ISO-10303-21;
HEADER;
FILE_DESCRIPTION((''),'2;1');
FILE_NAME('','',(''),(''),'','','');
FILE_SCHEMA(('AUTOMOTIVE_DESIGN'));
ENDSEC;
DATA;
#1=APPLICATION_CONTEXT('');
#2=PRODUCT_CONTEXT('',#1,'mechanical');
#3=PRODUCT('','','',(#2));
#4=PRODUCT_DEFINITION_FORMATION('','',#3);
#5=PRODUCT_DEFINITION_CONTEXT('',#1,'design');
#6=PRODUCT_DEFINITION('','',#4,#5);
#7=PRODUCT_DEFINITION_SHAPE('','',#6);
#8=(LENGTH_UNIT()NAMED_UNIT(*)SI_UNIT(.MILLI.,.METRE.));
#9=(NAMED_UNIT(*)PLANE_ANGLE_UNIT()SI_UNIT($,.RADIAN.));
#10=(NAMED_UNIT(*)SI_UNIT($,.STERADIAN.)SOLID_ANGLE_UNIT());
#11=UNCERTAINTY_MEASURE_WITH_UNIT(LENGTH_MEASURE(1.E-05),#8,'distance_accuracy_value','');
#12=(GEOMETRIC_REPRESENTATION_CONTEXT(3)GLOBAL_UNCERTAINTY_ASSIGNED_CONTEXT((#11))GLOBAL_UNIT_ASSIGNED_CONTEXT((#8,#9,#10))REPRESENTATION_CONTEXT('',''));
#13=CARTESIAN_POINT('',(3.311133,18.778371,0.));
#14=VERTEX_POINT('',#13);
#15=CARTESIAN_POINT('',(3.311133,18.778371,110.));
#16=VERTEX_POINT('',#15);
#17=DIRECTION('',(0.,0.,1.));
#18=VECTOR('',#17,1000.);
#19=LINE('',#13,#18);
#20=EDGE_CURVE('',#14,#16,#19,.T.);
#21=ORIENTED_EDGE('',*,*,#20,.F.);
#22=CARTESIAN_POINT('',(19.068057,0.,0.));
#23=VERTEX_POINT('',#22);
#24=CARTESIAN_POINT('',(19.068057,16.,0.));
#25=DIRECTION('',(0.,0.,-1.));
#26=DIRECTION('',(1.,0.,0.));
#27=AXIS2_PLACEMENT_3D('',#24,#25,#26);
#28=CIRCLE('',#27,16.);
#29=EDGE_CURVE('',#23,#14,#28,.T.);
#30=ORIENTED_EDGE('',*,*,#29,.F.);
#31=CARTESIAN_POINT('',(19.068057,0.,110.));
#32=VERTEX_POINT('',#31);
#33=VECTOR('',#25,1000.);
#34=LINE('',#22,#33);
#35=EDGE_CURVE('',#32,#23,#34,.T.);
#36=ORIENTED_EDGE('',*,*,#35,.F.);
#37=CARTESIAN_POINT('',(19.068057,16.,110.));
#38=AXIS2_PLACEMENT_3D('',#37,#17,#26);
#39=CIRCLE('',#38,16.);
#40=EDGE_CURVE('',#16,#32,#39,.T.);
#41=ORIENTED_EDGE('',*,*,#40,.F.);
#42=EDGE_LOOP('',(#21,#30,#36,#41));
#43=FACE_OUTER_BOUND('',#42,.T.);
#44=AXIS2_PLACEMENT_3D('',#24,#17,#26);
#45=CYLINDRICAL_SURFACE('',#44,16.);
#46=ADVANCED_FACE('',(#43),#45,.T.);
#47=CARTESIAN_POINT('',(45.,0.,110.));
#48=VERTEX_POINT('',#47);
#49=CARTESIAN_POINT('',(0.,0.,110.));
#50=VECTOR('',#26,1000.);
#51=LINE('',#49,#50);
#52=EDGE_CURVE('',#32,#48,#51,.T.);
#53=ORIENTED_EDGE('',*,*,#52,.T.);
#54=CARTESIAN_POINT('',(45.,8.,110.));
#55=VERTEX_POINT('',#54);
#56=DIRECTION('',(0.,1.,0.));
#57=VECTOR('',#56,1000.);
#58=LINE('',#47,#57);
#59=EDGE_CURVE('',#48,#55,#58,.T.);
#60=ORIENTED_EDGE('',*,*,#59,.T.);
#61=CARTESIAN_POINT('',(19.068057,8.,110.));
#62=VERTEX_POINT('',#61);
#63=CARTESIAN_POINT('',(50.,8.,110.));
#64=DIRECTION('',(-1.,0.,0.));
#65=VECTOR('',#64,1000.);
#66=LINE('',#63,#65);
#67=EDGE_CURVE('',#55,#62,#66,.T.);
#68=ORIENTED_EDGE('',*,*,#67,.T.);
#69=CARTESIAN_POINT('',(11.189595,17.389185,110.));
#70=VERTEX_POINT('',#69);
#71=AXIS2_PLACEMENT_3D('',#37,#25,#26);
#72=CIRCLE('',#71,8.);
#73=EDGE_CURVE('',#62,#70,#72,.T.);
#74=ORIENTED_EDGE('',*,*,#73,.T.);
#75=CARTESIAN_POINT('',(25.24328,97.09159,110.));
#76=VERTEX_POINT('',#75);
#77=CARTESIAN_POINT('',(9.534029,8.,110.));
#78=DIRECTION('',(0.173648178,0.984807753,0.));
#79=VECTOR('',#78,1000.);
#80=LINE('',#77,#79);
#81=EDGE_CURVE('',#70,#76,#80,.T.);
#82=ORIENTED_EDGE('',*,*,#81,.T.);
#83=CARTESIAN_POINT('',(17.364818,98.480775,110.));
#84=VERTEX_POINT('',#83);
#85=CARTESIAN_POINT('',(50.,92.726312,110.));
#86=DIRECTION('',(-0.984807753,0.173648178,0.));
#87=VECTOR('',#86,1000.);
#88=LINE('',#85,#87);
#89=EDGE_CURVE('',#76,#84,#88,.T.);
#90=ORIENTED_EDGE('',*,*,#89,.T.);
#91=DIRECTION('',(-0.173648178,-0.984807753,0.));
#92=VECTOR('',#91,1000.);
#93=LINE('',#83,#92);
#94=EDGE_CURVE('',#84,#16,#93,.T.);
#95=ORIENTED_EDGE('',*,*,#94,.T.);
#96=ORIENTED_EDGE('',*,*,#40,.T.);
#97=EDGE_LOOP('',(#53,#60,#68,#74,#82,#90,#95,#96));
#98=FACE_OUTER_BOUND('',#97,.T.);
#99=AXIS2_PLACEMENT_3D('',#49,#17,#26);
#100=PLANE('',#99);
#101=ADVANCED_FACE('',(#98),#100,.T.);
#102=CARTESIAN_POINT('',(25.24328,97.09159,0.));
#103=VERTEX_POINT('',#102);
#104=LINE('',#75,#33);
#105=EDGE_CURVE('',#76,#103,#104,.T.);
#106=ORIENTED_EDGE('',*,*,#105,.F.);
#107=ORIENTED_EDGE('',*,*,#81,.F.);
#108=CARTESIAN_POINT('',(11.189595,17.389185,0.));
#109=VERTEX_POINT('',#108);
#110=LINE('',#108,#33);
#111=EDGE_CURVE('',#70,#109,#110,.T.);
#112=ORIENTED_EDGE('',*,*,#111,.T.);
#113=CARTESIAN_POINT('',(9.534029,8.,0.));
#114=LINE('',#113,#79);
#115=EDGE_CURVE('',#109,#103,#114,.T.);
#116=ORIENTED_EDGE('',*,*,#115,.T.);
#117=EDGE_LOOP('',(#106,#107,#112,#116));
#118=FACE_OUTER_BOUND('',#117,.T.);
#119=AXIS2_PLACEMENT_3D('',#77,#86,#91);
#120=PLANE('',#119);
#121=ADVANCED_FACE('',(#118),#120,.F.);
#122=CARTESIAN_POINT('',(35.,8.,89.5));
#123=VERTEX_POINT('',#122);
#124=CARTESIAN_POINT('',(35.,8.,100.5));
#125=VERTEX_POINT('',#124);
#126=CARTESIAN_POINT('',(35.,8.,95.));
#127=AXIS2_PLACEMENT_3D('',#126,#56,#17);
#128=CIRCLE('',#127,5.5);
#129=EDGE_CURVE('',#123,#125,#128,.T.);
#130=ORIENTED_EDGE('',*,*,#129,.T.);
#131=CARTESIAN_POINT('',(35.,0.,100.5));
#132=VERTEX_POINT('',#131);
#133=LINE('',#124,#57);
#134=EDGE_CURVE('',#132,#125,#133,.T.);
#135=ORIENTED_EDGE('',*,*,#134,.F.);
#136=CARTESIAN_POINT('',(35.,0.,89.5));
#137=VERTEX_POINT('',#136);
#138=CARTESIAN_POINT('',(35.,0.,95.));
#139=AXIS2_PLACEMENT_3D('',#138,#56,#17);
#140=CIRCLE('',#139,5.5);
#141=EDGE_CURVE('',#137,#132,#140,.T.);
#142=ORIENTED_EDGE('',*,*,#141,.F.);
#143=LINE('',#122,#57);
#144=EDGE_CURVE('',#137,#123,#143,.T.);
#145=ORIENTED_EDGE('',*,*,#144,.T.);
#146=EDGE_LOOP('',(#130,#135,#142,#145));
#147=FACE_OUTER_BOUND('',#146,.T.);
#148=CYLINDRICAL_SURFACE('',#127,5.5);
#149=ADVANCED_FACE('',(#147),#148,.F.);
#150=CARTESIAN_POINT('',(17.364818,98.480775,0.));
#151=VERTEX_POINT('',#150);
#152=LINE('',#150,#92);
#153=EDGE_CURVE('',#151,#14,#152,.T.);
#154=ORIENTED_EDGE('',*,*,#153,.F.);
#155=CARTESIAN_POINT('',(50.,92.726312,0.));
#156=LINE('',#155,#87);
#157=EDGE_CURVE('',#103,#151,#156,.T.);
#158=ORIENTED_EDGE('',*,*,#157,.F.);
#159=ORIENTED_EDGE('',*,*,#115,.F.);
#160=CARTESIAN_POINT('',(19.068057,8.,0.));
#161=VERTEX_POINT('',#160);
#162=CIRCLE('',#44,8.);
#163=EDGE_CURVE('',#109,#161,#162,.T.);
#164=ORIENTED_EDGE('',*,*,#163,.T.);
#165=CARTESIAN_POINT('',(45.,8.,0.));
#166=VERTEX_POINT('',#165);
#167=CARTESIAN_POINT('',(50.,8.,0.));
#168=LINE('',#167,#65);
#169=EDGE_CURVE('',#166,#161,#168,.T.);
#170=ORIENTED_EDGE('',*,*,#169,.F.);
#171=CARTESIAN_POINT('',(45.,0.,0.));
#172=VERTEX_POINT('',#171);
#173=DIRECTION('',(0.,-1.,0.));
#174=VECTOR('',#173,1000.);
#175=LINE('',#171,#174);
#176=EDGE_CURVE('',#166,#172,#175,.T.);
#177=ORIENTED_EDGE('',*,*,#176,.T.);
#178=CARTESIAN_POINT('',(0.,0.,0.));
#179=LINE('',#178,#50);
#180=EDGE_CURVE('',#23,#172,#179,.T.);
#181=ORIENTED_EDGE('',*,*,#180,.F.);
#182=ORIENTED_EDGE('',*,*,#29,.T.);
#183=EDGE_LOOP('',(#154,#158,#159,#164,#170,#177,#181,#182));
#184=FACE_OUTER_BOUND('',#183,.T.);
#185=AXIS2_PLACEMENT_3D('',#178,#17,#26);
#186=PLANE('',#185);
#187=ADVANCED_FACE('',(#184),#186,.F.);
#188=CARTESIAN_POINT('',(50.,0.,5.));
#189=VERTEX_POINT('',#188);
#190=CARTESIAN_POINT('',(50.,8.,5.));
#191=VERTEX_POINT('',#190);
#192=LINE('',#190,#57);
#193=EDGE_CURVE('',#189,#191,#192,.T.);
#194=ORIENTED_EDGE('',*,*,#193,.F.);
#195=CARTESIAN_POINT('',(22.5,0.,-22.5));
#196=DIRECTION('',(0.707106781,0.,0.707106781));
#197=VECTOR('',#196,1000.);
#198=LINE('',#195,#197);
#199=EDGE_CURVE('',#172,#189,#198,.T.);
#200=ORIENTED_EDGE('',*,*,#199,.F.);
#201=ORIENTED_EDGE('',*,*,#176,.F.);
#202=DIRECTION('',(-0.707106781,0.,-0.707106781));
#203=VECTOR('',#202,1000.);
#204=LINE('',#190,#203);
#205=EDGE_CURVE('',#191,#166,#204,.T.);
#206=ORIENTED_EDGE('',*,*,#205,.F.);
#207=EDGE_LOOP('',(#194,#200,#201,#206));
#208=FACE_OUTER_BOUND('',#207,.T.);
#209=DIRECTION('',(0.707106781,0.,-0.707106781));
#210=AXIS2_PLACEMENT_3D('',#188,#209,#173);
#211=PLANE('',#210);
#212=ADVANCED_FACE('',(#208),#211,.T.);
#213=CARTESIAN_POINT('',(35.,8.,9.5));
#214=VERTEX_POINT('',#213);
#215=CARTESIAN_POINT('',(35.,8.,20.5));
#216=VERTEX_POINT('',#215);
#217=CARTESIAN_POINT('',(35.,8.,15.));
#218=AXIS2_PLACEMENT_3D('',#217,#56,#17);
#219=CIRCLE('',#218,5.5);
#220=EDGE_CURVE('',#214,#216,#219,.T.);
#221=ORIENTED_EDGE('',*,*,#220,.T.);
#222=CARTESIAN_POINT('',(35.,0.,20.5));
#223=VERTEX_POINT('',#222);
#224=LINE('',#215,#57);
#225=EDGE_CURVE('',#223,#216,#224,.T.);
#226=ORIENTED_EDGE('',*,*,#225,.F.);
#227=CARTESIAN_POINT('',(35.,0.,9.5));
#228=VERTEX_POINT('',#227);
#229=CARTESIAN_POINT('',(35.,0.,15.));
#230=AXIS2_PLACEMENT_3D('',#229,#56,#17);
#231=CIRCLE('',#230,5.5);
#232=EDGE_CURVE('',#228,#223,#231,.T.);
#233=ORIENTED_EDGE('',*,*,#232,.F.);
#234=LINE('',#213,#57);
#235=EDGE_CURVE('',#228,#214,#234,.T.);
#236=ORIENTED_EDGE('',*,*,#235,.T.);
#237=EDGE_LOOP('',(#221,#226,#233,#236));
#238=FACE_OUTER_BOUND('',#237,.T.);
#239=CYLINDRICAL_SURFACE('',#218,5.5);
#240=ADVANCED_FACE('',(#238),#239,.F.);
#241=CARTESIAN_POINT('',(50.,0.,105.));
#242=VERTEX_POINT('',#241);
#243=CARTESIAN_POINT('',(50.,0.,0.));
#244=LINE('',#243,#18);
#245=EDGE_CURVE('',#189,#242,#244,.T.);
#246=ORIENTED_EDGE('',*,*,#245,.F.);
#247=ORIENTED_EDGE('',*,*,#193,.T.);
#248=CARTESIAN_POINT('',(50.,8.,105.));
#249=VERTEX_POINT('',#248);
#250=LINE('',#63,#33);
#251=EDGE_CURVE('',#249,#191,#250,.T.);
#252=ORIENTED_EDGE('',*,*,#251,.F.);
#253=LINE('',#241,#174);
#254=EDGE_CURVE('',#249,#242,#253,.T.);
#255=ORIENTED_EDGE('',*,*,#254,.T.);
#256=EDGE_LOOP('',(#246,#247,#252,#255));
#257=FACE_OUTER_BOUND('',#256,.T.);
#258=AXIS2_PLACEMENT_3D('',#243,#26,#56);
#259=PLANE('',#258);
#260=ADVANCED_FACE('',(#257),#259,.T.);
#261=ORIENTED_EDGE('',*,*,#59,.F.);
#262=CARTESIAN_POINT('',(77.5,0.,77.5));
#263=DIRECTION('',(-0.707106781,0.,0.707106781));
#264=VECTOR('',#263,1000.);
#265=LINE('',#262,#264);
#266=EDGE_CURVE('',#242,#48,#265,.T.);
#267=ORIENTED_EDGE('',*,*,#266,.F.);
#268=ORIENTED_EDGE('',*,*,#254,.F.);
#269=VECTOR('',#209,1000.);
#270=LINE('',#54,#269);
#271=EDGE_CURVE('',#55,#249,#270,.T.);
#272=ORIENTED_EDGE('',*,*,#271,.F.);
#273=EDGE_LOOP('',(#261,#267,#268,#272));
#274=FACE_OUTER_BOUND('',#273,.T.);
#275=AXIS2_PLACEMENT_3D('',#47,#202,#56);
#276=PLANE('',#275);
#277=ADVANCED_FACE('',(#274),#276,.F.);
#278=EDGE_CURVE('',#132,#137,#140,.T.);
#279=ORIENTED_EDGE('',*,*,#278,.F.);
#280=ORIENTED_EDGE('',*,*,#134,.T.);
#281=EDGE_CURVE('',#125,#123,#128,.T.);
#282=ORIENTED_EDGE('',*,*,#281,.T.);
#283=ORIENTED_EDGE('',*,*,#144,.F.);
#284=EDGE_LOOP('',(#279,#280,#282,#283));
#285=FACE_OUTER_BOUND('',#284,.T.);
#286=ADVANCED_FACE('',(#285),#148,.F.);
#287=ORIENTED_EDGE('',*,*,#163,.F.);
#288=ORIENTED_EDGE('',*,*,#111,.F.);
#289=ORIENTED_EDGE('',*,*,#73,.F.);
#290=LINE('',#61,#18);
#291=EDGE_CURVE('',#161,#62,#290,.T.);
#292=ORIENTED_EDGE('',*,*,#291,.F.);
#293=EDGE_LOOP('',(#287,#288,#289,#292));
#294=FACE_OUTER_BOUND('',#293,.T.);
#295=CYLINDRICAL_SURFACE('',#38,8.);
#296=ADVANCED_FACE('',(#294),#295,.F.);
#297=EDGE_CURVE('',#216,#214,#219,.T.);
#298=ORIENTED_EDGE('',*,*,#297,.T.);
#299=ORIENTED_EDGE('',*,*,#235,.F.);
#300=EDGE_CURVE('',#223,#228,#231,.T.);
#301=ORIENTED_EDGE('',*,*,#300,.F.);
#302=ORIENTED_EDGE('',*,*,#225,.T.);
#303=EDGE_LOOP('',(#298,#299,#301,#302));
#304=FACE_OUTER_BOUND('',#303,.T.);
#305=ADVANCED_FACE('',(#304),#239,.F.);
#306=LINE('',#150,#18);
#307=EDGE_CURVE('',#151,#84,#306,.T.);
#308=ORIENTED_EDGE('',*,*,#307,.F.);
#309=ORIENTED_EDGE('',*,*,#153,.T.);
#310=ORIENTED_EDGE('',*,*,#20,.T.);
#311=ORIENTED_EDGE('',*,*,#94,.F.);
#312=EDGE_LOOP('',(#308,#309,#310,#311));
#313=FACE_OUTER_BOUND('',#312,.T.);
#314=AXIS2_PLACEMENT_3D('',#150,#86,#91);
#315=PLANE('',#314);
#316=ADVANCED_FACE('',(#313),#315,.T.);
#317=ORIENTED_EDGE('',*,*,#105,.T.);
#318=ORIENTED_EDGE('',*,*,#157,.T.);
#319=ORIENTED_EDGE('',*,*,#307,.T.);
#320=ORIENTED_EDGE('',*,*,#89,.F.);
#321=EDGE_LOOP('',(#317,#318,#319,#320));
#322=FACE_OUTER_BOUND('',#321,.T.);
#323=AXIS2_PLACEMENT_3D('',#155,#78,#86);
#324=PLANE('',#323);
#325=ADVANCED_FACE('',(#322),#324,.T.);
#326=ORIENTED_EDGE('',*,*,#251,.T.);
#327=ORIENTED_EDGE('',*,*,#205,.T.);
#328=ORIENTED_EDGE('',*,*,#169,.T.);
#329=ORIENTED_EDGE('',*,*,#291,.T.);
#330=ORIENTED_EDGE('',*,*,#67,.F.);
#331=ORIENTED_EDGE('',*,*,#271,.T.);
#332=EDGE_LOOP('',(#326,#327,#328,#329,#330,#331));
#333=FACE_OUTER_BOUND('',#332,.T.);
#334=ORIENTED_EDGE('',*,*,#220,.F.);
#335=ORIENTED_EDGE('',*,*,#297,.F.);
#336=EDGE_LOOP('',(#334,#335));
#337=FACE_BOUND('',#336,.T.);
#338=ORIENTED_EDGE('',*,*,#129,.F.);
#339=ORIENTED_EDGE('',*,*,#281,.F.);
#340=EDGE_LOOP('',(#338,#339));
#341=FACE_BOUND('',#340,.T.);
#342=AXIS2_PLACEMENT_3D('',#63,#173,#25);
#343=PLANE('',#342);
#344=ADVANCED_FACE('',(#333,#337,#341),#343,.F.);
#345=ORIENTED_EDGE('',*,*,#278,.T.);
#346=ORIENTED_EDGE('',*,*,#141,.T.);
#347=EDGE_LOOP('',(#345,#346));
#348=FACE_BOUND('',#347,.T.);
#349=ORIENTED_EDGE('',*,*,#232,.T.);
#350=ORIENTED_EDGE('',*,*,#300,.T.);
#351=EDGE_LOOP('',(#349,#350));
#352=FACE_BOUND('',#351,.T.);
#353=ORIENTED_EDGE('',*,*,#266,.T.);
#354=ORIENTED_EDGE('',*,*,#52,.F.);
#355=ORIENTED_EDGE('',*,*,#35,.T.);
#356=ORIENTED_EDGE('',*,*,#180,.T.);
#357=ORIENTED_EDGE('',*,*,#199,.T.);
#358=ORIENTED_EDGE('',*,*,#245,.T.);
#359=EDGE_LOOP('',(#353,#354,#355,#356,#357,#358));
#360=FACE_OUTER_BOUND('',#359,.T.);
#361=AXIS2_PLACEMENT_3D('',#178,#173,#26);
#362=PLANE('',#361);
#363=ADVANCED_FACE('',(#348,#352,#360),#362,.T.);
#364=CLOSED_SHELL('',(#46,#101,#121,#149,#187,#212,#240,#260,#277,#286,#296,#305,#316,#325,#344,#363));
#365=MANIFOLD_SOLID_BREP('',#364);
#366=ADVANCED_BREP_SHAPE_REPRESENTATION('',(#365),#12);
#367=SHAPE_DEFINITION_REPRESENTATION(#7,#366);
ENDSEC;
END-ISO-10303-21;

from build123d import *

# Parameters (mm, degrees)
EXTRUDE_1_DEPTH         = 110
CUT_EXTRUDE_1_DEPTH     = 156.879643007
HOLE_WIZARD_11_0_11_1_D = 11
CHAMFER_1_SIZE          = 5
FILLET_1_R              = 8
FILLET_2_R              = 16


with BuildPart() as part:
    # 草图1 → 凸台-拉伸1 (new body)
    with BuildSketch(Plane.XY.offset(110)):
        Polygon((50, 0), (50, 92.726312153), (17.364817767, 98.480775301), (0, 0), align=None)
    extrude(amount=-EXTRUDE_1_DEPTH)

    # 草图2 → 切除-拉伸1 (cut, through all)
    with BuildSketch(Plane(origin=(0, 0, 0), x_dir=(-1, 0, 0), z_dir=(0, 0, -1))):
        Polygon((-9.534028741, 8), (-25.243279791, 97.09158988), (-50, 92.726312153), (-50, 8), align=None)
    extrude(amount=-CUT_EXTRUDE_1_DEPTH, mode=Mode.SUBTRACT)

    # Ø11.0 (11) 直径孔1 (through all)
    with Locations(Plane(origin=(0, 8, 0), x_dir=(1, 0, 0), z_dir=(0, 1, 0))):
        with Locations((35, -15), (35, -95)):
            Hole(HOLE_WIZARD_11_0_11_1_D / 2)

    # 倒角1
    chamfer_1_edges = [part.edges().sort_by_distance(p)[0] for p in [
        (50, 4, 110),
        (50, 4, 0),
    ]]
    chamfer(chamfer_1_edges, length=CHAMFER_1_SIZE)

    # 圆角1
    fillet_1_edges = [part.edges().sort_by_distance(p)[0] for p in [
        (9.534028741, 8, 55),
    ]]
    fillet(fillet_1_edges, radius=FILLET_1_R)

    # 圆角2
    fillet_2_edges = [part.edges().sort_by_distance(p)[0] for p in [
        (0, 0, 55),
    ]]
    fillet(fillet_2_edges, radius=FILLET_2_R)


solid = part.part
